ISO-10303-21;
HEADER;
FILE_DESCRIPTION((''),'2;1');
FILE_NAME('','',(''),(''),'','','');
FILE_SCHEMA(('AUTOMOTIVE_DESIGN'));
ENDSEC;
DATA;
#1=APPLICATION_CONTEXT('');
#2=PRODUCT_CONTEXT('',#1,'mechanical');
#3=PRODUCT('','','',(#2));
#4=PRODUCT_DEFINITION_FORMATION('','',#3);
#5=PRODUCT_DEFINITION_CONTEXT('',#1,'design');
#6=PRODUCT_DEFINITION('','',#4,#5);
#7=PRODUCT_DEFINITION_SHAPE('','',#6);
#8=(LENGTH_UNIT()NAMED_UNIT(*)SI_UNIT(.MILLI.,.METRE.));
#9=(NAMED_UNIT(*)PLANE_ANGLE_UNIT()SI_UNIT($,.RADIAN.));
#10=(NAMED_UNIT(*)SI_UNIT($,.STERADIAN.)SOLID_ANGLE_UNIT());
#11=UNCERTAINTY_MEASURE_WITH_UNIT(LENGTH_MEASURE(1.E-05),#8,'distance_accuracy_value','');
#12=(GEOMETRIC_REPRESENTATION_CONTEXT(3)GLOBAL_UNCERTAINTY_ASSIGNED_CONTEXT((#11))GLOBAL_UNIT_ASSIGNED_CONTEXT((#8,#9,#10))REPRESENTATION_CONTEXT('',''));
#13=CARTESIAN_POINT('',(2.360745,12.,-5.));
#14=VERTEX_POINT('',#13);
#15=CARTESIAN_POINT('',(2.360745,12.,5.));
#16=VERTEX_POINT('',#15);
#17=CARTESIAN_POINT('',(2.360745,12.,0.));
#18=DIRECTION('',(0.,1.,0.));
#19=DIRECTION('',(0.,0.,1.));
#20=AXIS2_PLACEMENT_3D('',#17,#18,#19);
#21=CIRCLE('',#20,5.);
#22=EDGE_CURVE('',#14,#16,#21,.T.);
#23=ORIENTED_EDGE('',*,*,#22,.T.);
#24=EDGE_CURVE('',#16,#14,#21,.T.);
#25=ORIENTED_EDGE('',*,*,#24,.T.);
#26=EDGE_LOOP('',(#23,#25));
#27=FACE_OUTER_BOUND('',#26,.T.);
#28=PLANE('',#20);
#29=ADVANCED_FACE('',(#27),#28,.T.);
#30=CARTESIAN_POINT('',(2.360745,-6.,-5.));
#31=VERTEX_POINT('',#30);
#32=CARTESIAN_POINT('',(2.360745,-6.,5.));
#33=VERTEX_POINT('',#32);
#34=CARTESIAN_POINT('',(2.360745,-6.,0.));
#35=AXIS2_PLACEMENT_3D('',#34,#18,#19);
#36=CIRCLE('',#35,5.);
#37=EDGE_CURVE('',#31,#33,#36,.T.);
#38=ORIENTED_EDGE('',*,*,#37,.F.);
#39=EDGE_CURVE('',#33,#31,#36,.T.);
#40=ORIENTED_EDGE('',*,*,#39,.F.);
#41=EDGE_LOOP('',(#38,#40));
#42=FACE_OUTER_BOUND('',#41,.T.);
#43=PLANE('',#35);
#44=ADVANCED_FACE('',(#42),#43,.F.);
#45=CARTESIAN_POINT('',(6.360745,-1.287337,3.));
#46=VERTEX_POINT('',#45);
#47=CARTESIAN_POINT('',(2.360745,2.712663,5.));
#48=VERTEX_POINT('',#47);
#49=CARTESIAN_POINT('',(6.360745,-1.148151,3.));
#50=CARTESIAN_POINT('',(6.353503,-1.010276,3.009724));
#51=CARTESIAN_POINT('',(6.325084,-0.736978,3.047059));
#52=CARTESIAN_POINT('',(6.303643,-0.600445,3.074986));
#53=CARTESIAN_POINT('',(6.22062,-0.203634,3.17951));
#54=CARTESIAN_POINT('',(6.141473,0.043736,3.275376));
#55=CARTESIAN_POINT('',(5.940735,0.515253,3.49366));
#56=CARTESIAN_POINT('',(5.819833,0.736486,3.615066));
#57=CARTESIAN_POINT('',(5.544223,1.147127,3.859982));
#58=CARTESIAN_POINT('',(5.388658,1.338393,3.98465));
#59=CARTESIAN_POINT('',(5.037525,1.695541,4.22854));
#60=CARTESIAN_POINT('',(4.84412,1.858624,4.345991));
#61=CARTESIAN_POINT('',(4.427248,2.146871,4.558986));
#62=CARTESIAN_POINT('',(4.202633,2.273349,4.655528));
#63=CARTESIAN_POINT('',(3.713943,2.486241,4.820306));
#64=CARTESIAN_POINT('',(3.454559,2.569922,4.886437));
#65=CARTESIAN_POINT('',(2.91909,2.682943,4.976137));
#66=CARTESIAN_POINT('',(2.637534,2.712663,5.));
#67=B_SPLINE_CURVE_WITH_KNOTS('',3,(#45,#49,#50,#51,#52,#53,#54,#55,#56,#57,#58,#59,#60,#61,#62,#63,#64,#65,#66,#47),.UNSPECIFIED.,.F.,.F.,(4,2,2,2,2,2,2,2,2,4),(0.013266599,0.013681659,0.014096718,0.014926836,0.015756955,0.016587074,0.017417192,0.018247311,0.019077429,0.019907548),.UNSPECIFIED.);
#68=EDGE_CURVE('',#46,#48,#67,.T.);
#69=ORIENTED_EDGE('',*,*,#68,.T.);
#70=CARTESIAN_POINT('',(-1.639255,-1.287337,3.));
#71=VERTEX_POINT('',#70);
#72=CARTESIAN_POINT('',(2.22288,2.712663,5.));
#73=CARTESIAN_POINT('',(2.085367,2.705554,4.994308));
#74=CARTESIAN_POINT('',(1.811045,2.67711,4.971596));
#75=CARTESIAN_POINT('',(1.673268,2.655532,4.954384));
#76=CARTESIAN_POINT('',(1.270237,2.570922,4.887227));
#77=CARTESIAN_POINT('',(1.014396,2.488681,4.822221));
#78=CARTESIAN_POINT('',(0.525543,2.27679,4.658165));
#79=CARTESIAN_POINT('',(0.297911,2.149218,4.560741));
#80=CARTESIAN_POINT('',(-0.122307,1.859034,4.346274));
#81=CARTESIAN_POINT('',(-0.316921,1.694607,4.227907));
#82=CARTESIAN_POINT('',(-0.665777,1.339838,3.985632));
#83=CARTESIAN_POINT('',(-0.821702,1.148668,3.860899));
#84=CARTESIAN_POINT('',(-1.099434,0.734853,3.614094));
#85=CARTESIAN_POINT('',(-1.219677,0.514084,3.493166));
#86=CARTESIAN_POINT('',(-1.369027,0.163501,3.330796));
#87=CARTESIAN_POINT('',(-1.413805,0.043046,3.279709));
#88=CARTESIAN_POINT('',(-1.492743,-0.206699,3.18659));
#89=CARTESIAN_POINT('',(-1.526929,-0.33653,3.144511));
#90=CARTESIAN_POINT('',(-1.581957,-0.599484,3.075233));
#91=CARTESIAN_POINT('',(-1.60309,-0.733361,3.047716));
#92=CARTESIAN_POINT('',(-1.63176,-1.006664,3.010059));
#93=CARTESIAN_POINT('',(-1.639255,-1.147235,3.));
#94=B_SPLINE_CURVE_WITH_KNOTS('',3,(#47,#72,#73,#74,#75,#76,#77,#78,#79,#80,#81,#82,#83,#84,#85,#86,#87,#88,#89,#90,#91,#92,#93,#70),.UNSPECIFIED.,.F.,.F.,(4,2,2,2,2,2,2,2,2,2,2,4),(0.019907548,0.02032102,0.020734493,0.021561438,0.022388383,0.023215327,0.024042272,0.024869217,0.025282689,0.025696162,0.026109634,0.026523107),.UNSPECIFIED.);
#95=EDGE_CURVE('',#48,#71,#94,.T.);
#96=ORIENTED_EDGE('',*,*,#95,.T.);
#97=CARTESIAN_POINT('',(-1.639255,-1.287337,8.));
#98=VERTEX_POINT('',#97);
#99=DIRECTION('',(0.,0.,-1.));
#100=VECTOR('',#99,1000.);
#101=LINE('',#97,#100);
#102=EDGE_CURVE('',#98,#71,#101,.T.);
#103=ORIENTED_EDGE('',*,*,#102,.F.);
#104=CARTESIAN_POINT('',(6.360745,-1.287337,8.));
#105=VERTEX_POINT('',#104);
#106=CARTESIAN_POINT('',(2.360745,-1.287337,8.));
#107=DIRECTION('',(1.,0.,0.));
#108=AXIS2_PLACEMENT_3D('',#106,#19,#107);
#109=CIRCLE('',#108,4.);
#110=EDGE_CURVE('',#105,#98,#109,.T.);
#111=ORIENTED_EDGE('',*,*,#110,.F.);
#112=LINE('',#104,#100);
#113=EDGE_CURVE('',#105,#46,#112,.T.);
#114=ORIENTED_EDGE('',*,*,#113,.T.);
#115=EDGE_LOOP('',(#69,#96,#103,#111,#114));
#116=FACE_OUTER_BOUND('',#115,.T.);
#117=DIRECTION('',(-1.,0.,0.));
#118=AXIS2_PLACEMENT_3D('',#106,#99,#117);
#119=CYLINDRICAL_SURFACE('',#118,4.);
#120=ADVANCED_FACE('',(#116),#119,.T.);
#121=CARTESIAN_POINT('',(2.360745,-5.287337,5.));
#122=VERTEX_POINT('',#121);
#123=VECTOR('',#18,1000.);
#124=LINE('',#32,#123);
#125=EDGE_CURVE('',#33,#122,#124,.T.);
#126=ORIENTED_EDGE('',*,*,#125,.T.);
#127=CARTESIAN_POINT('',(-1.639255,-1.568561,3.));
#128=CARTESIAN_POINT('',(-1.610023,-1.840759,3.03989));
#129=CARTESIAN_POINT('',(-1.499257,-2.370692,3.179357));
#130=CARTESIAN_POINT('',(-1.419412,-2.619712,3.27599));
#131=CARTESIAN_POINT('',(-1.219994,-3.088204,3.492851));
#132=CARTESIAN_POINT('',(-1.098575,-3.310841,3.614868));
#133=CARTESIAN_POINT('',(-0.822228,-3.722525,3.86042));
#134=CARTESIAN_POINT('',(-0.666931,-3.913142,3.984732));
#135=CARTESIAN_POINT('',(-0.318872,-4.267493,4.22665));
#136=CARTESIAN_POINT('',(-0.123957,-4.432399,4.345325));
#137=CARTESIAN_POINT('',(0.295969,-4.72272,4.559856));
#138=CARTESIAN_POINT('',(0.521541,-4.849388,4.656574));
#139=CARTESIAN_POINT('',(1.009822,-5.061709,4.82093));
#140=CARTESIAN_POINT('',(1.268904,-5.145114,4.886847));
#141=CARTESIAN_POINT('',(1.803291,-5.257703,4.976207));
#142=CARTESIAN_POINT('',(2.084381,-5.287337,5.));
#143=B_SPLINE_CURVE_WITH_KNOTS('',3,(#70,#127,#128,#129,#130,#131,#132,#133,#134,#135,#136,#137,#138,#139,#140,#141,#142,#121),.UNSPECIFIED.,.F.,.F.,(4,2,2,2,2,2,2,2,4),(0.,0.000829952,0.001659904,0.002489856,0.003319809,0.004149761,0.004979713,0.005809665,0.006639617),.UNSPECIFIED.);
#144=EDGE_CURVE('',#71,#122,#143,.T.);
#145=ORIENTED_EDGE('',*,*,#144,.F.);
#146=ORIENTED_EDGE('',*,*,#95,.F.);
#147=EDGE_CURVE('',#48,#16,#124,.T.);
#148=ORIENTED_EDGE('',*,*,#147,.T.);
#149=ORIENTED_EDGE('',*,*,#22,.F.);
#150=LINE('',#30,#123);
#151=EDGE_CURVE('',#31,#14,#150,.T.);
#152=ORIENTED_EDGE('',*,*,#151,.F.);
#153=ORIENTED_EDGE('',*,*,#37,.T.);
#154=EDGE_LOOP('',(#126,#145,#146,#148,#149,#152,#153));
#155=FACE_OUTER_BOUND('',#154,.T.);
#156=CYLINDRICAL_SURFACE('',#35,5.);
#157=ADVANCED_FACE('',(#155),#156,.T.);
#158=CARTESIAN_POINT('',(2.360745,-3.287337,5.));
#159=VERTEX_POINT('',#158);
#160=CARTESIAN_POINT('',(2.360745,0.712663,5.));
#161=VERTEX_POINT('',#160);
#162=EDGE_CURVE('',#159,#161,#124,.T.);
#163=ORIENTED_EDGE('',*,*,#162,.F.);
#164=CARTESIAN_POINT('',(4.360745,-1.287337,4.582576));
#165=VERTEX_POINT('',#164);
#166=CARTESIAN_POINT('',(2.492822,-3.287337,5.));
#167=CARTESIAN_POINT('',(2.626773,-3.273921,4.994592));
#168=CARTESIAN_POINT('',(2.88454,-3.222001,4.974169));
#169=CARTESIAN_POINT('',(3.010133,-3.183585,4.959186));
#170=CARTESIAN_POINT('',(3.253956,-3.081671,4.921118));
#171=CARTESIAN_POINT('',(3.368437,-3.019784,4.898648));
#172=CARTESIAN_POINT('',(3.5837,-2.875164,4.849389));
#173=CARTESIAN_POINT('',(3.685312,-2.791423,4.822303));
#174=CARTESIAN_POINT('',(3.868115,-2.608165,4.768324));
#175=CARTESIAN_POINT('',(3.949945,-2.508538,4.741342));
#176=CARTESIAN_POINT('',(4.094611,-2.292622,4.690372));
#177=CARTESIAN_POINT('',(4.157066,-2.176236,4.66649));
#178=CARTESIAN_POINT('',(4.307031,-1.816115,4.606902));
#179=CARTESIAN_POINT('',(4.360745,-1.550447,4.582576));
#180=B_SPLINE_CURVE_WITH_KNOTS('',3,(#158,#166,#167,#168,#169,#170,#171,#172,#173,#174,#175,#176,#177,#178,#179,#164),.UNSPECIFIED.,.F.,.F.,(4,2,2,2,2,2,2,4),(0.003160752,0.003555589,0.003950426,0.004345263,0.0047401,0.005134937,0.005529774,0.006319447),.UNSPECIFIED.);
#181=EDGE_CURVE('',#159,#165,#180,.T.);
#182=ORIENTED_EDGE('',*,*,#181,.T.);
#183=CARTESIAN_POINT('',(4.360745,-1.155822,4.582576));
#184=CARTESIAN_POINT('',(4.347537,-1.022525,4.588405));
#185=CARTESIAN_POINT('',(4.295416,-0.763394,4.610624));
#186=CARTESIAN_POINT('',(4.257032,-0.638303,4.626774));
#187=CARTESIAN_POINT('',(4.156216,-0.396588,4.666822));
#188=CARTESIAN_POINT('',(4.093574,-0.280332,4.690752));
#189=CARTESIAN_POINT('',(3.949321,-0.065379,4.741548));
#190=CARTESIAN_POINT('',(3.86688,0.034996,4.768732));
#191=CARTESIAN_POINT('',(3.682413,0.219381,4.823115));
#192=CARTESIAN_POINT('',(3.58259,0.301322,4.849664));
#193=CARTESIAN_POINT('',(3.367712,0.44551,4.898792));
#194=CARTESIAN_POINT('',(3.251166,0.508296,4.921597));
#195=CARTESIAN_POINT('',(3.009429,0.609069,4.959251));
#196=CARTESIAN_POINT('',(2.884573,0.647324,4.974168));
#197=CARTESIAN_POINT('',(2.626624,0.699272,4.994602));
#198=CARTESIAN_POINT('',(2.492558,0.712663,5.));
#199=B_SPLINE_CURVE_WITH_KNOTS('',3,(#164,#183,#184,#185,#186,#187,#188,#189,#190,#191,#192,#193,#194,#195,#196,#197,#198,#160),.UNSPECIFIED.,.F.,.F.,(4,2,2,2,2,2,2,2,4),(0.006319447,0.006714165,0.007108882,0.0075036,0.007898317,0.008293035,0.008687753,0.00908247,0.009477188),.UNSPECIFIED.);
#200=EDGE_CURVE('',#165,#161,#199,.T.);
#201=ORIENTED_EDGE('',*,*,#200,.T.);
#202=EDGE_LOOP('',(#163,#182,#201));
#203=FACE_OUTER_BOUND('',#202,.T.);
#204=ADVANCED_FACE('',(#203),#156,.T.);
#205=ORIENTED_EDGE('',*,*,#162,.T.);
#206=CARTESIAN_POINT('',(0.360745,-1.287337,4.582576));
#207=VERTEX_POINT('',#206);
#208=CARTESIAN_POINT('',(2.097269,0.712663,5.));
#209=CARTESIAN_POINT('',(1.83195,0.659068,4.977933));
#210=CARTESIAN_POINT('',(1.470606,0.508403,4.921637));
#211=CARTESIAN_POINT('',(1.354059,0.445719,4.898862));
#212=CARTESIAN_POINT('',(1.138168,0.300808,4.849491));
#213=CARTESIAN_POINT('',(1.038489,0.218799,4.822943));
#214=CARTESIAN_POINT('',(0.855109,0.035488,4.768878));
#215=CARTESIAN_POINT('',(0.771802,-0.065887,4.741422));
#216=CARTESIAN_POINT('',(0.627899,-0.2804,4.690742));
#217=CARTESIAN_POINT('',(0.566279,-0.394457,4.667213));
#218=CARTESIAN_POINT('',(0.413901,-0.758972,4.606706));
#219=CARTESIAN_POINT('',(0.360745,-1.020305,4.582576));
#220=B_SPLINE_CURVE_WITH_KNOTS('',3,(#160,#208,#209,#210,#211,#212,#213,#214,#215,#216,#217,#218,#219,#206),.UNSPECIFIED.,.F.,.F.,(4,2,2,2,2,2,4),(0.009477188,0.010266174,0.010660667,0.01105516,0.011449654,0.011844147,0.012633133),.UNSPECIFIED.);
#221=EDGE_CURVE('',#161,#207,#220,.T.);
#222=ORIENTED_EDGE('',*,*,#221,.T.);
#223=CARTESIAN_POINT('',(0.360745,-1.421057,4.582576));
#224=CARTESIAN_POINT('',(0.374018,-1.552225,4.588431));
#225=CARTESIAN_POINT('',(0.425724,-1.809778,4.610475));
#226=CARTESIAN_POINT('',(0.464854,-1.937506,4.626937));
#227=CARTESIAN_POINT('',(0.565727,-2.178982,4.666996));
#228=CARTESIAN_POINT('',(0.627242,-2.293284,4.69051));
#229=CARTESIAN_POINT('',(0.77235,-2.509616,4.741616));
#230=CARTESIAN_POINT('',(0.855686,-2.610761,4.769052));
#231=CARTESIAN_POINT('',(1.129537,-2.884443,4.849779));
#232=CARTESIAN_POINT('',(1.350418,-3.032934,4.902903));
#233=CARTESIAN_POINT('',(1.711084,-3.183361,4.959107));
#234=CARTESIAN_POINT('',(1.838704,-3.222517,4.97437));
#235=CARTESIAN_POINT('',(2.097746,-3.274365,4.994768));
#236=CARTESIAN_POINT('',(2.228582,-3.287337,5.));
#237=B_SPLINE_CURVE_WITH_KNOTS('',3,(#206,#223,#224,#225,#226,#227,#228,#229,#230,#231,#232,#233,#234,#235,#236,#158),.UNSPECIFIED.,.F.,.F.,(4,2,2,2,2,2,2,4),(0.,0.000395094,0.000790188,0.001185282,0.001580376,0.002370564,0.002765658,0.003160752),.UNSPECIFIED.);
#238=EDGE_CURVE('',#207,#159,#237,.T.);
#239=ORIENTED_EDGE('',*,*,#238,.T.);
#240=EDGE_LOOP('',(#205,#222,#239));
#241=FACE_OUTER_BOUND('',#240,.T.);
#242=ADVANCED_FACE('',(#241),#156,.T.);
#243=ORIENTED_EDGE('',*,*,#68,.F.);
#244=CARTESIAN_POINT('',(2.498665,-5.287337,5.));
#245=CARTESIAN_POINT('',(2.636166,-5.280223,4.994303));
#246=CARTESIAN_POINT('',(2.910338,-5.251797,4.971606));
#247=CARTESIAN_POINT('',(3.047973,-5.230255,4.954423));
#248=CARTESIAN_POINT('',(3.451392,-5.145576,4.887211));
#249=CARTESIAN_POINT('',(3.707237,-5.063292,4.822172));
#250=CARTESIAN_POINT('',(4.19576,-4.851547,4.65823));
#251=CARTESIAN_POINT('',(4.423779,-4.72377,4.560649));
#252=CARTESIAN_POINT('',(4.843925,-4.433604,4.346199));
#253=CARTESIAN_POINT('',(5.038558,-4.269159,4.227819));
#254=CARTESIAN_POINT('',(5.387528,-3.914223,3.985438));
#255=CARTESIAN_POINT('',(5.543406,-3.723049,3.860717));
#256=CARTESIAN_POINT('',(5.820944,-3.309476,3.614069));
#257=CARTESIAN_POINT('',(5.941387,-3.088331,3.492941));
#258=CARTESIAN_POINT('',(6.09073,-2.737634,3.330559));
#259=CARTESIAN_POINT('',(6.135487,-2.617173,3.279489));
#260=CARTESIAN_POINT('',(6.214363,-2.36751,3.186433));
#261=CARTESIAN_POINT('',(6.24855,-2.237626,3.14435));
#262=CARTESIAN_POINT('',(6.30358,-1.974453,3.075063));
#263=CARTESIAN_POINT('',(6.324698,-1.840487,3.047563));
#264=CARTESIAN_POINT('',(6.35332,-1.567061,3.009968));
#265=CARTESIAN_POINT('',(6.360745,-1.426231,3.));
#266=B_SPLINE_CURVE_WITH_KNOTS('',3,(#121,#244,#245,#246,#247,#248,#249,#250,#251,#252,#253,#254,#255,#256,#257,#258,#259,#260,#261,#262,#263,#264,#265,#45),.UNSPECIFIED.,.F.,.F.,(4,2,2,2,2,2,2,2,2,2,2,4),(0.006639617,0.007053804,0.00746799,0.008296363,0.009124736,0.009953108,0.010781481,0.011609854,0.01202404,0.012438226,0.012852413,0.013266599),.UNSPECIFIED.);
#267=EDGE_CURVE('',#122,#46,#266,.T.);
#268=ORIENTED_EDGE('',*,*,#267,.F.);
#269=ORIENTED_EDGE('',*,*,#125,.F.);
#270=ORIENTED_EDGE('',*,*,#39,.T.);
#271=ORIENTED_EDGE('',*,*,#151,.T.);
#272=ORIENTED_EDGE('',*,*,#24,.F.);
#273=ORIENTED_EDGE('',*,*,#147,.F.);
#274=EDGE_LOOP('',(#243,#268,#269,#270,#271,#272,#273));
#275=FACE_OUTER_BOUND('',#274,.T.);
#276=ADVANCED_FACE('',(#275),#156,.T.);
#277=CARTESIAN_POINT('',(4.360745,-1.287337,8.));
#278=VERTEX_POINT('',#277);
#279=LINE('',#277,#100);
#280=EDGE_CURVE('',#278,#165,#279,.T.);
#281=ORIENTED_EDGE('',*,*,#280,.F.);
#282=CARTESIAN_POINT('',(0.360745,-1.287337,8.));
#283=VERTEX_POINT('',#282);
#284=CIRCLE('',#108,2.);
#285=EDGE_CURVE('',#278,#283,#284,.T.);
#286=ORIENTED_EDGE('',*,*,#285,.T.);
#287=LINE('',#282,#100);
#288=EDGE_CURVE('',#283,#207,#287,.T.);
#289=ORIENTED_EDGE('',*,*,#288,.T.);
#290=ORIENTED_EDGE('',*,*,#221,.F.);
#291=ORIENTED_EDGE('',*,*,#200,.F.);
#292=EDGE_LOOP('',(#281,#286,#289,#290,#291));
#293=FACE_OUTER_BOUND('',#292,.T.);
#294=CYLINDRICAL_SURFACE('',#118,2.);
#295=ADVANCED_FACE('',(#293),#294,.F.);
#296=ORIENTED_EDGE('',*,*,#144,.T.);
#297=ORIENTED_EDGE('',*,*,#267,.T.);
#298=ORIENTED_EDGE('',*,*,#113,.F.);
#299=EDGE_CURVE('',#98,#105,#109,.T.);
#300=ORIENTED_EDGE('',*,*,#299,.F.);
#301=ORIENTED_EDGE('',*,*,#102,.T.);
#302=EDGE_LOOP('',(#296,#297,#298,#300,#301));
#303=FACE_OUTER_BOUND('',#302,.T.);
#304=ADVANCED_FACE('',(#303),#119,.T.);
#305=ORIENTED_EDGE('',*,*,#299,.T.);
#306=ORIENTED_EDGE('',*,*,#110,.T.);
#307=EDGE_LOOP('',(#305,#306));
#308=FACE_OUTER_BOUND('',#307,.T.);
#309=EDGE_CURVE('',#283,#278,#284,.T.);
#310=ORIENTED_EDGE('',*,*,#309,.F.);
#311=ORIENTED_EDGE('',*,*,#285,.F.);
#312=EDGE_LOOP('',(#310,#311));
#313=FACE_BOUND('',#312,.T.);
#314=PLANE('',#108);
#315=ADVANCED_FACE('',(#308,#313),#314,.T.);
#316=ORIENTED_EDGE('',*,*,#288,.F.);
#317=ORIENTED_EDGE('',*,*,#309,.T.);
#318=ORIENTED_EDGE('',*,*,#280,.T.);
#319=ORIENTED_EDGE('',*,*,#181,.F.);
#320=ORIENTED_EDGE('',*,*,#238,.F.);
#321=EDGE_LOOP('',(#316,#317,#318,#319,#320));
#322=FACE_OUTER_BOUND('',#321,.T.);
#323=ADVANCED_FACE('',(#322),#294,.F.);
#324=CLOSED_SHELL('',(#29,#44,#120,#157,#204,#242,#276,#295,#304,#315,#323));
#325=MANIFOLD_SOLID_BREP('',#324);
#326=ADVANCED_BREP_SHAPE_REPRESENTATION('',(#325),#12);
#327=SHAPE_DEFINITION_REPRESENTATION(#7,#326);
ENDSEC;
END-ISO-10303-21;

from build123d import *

# Parameters (mm, degrees)
SKETCH_1_R           = 4
SKETCH_1_R_2         = 2
EXTRUDE_1_DEPTH      = 8
EXTRUDE_2_DEPTH      = 12
EXTRUDE_2_DEPTH_BACK = 6
SKETCH_3_R           = 5


with BuildPart() as part:
    # 草图1 → 凸台-拉伸1 (new body)
    with BuildSketch(Plane.XY):
        with Locations((2.360745364, -1.287337305)):
            Circle(SKETCH_1_R)
        with Locations((2.360745364, -1.287337305)):
            Circle(SKETCH_1_R_2, mode=Mode.SUBTRACT)
    extrude(amount=EXTRUDE_1_DEPTH)

    # 草图3 → 凸台-拉伸2 (add, two sides: drawn at the far end of the back side and taken through both)
    with BuildSketch(Plane(origin=(0, 0, 0), x_dir=(1, 0, 0), z_dir=(0, 1, 0)).offset(-EXTRUDE_2_DEPTH_BACK)):
        with Locations(Location((2.360745364, 0, 0), (0, 0, 270))):
            Circle(SKETCH_3_R)
    extrude(amount=EXTRUDE_2_DEPTH + EXTRUDE_2_DEPTH_BACK)


solid = part.part
